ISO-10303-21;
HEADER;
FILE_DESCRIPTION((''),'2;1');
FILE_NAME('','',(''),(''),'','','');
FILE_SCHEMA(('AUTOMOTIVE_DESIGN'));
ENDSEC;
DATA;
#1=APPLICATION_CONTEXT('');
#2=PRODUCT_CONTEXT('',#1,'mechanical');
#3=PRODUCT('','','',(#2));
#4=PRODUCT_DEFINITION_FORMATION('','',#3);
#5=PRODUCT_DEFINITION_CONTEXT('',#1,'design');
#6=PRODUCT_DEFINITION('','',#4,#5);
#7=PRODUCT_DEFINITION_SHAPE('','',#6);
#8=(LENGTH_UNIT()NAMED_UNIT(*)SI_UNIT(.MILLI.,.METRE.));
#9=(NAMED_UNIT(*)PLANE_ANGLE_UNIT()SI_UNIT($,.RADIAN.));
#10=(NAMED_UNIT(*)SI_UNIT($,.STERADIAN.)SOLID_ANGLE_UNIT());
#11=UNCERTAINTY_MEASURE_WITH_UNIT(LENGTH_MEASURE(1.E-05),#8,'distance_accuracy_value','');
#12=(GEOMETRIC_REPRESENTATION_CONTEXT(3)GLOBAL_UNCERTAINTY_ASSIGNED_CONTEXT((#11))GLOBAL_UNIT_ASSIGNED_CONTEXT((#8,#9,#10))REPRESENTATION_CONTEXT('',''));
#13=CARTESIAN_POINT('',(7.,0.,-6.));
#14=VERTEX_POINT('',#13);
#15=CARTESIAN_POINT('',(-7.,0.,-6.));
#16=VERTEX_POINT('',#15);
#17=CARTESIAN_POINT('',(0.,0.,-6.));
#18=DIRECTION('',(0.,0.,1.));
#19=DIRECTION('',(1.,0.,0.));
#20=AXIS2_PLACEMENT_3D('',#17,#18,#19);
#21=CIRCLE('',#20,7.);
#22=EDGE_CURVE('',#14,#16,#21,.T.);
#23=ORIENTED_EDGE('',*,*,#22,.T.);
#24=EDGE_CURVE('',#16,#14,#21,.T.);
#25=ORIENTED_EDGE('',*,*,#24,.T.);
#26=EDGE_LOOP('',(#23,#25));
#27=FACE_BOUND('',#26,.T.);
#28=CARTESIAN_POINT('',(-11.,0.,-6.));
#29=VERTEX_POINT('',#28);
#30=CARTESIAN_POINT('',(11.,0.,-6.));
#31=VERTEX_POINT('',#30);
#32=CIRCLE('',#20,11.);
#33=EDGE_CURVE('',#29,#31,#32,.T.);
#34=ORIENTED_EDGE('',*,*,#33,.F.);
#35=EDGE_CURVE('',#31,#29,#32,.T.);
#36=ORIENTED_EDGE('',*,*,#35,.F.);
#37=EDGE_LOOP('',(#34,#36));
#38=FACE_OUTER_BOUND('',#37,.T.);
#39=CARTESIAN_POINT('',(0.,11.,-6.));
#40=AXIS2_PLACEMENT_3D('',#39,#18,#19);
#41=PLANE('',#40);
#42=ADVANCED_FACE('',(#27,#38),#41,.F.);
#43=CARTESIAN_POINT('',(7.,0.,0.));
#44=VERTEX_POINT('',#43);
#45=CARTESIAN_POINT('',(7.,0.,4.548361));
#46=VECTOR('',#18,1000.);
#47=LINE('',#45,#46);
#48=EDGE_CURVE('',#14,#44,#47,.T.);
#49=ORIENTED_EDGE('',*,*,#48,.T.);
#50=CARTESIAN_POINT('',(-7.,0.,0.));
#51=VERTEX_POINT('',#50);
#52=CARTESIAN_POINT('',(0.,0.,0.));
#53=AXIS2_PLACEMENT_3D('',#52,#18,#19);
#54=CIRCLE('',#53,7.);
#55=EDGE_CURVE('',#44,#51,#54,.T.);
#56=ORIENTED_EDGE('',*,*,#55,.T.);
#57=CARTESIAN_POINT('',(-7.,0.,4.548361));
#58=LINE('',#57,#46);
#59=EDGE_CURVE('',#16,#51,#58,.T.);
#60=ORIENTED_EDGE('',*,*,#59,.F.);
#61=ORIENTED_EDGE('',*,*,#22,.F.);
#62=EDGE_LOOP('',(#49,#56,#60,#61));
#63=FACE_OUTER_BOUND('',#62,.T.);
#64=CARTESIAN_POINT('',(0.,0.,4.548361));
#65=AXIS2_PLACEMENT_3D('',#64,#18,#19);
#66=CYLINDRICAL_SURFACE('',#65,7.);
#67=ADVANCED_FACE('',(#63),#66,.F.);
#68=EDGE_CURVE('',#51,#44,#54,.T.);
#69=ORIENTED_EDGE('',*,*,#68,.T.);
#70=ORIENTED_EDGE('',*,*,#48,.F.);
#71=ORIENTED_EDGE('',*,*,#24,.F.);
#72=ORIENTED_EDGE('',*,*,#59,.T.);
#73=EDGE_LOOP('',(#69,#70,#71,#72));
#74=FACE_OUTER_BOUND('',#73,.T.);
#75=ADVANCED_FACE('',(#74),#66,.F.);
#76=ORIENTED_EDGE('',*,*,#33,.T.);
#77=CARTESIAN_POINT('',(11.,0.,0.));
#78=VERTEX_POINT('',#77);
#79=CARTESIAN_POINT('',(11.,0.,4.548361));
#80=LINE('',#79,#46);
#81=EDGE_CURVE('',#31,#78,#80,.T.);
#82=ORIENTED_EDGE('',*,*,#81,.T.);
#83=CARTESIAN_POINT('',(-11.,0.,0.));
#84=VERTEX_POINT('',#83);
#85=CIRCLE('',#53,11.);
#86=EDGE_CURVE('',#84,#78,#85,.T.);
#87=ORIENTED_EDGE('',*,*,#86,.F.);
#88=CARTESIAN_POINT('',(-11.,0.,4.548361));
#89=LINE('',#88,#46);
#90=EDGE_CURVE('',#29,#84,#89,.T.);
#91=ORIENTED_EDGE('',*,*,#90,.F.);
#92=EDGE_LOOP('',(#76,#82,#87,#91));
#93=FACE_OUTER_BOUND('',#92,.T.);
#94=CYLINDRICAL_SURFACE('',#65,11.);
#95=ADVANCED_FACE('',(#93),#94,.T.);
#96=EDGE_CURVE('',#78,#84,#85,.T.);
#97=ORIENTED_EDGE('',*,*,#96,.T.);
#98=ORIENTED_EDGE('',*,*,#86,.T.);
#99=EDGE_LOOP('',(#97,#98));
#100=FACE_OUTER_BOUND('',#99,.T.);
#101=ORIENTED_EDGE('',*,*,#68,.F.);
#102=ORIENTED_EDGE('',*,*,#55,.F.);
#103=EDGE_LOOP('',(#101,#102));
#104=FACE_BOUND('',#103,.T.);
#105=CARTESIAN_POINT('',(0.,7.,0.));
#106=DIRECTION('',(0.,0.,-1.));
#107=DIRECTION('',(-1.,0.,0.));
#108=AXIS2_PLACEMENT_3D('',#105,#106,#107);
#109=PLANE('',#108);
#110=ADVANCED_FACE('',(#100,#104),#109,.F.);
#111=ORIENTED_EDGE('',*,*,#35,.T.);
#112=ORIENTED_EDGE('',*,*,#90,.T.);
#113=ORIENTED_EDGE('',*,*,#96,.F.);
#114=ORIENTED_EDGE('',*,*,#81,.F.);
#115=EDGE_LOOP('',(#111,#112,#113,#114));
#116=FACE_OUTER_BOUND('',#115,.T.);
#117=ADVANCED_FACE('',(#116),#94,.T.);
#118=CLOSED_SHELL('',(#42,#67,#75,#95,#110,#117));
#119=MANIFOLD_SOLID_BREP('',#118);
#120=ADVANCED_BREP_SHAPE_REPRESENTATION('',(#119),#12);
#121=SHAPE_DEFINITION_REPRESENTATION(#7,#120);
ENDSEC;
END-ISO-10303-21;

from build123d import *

# Parameters (mm, degrees)
SKETCH1_W = 6
SKETCH1_H = 4


with BuildPart() as part:
    # Sketch1 → Revolve1 (revolve)
    with BuildSketch(Plane(origin=(0, 0, 0), x_dir=(0, 0, -1), z_dir=(1, 0, 0)), mode=Mode.PRIVATE) as revolve1_sk:
        with Locations((3, 9)):
            Rectangle(SKETCH1_W, SKETCH1_H)
    revolve(revolve1_sk.sketch.rotate(Axis((0, 0, 4.548360851), (0, 0, -1)), 90), axis=Axis((0, 0, 4.548360851), (0, 0, -1)))


solid = part.part
